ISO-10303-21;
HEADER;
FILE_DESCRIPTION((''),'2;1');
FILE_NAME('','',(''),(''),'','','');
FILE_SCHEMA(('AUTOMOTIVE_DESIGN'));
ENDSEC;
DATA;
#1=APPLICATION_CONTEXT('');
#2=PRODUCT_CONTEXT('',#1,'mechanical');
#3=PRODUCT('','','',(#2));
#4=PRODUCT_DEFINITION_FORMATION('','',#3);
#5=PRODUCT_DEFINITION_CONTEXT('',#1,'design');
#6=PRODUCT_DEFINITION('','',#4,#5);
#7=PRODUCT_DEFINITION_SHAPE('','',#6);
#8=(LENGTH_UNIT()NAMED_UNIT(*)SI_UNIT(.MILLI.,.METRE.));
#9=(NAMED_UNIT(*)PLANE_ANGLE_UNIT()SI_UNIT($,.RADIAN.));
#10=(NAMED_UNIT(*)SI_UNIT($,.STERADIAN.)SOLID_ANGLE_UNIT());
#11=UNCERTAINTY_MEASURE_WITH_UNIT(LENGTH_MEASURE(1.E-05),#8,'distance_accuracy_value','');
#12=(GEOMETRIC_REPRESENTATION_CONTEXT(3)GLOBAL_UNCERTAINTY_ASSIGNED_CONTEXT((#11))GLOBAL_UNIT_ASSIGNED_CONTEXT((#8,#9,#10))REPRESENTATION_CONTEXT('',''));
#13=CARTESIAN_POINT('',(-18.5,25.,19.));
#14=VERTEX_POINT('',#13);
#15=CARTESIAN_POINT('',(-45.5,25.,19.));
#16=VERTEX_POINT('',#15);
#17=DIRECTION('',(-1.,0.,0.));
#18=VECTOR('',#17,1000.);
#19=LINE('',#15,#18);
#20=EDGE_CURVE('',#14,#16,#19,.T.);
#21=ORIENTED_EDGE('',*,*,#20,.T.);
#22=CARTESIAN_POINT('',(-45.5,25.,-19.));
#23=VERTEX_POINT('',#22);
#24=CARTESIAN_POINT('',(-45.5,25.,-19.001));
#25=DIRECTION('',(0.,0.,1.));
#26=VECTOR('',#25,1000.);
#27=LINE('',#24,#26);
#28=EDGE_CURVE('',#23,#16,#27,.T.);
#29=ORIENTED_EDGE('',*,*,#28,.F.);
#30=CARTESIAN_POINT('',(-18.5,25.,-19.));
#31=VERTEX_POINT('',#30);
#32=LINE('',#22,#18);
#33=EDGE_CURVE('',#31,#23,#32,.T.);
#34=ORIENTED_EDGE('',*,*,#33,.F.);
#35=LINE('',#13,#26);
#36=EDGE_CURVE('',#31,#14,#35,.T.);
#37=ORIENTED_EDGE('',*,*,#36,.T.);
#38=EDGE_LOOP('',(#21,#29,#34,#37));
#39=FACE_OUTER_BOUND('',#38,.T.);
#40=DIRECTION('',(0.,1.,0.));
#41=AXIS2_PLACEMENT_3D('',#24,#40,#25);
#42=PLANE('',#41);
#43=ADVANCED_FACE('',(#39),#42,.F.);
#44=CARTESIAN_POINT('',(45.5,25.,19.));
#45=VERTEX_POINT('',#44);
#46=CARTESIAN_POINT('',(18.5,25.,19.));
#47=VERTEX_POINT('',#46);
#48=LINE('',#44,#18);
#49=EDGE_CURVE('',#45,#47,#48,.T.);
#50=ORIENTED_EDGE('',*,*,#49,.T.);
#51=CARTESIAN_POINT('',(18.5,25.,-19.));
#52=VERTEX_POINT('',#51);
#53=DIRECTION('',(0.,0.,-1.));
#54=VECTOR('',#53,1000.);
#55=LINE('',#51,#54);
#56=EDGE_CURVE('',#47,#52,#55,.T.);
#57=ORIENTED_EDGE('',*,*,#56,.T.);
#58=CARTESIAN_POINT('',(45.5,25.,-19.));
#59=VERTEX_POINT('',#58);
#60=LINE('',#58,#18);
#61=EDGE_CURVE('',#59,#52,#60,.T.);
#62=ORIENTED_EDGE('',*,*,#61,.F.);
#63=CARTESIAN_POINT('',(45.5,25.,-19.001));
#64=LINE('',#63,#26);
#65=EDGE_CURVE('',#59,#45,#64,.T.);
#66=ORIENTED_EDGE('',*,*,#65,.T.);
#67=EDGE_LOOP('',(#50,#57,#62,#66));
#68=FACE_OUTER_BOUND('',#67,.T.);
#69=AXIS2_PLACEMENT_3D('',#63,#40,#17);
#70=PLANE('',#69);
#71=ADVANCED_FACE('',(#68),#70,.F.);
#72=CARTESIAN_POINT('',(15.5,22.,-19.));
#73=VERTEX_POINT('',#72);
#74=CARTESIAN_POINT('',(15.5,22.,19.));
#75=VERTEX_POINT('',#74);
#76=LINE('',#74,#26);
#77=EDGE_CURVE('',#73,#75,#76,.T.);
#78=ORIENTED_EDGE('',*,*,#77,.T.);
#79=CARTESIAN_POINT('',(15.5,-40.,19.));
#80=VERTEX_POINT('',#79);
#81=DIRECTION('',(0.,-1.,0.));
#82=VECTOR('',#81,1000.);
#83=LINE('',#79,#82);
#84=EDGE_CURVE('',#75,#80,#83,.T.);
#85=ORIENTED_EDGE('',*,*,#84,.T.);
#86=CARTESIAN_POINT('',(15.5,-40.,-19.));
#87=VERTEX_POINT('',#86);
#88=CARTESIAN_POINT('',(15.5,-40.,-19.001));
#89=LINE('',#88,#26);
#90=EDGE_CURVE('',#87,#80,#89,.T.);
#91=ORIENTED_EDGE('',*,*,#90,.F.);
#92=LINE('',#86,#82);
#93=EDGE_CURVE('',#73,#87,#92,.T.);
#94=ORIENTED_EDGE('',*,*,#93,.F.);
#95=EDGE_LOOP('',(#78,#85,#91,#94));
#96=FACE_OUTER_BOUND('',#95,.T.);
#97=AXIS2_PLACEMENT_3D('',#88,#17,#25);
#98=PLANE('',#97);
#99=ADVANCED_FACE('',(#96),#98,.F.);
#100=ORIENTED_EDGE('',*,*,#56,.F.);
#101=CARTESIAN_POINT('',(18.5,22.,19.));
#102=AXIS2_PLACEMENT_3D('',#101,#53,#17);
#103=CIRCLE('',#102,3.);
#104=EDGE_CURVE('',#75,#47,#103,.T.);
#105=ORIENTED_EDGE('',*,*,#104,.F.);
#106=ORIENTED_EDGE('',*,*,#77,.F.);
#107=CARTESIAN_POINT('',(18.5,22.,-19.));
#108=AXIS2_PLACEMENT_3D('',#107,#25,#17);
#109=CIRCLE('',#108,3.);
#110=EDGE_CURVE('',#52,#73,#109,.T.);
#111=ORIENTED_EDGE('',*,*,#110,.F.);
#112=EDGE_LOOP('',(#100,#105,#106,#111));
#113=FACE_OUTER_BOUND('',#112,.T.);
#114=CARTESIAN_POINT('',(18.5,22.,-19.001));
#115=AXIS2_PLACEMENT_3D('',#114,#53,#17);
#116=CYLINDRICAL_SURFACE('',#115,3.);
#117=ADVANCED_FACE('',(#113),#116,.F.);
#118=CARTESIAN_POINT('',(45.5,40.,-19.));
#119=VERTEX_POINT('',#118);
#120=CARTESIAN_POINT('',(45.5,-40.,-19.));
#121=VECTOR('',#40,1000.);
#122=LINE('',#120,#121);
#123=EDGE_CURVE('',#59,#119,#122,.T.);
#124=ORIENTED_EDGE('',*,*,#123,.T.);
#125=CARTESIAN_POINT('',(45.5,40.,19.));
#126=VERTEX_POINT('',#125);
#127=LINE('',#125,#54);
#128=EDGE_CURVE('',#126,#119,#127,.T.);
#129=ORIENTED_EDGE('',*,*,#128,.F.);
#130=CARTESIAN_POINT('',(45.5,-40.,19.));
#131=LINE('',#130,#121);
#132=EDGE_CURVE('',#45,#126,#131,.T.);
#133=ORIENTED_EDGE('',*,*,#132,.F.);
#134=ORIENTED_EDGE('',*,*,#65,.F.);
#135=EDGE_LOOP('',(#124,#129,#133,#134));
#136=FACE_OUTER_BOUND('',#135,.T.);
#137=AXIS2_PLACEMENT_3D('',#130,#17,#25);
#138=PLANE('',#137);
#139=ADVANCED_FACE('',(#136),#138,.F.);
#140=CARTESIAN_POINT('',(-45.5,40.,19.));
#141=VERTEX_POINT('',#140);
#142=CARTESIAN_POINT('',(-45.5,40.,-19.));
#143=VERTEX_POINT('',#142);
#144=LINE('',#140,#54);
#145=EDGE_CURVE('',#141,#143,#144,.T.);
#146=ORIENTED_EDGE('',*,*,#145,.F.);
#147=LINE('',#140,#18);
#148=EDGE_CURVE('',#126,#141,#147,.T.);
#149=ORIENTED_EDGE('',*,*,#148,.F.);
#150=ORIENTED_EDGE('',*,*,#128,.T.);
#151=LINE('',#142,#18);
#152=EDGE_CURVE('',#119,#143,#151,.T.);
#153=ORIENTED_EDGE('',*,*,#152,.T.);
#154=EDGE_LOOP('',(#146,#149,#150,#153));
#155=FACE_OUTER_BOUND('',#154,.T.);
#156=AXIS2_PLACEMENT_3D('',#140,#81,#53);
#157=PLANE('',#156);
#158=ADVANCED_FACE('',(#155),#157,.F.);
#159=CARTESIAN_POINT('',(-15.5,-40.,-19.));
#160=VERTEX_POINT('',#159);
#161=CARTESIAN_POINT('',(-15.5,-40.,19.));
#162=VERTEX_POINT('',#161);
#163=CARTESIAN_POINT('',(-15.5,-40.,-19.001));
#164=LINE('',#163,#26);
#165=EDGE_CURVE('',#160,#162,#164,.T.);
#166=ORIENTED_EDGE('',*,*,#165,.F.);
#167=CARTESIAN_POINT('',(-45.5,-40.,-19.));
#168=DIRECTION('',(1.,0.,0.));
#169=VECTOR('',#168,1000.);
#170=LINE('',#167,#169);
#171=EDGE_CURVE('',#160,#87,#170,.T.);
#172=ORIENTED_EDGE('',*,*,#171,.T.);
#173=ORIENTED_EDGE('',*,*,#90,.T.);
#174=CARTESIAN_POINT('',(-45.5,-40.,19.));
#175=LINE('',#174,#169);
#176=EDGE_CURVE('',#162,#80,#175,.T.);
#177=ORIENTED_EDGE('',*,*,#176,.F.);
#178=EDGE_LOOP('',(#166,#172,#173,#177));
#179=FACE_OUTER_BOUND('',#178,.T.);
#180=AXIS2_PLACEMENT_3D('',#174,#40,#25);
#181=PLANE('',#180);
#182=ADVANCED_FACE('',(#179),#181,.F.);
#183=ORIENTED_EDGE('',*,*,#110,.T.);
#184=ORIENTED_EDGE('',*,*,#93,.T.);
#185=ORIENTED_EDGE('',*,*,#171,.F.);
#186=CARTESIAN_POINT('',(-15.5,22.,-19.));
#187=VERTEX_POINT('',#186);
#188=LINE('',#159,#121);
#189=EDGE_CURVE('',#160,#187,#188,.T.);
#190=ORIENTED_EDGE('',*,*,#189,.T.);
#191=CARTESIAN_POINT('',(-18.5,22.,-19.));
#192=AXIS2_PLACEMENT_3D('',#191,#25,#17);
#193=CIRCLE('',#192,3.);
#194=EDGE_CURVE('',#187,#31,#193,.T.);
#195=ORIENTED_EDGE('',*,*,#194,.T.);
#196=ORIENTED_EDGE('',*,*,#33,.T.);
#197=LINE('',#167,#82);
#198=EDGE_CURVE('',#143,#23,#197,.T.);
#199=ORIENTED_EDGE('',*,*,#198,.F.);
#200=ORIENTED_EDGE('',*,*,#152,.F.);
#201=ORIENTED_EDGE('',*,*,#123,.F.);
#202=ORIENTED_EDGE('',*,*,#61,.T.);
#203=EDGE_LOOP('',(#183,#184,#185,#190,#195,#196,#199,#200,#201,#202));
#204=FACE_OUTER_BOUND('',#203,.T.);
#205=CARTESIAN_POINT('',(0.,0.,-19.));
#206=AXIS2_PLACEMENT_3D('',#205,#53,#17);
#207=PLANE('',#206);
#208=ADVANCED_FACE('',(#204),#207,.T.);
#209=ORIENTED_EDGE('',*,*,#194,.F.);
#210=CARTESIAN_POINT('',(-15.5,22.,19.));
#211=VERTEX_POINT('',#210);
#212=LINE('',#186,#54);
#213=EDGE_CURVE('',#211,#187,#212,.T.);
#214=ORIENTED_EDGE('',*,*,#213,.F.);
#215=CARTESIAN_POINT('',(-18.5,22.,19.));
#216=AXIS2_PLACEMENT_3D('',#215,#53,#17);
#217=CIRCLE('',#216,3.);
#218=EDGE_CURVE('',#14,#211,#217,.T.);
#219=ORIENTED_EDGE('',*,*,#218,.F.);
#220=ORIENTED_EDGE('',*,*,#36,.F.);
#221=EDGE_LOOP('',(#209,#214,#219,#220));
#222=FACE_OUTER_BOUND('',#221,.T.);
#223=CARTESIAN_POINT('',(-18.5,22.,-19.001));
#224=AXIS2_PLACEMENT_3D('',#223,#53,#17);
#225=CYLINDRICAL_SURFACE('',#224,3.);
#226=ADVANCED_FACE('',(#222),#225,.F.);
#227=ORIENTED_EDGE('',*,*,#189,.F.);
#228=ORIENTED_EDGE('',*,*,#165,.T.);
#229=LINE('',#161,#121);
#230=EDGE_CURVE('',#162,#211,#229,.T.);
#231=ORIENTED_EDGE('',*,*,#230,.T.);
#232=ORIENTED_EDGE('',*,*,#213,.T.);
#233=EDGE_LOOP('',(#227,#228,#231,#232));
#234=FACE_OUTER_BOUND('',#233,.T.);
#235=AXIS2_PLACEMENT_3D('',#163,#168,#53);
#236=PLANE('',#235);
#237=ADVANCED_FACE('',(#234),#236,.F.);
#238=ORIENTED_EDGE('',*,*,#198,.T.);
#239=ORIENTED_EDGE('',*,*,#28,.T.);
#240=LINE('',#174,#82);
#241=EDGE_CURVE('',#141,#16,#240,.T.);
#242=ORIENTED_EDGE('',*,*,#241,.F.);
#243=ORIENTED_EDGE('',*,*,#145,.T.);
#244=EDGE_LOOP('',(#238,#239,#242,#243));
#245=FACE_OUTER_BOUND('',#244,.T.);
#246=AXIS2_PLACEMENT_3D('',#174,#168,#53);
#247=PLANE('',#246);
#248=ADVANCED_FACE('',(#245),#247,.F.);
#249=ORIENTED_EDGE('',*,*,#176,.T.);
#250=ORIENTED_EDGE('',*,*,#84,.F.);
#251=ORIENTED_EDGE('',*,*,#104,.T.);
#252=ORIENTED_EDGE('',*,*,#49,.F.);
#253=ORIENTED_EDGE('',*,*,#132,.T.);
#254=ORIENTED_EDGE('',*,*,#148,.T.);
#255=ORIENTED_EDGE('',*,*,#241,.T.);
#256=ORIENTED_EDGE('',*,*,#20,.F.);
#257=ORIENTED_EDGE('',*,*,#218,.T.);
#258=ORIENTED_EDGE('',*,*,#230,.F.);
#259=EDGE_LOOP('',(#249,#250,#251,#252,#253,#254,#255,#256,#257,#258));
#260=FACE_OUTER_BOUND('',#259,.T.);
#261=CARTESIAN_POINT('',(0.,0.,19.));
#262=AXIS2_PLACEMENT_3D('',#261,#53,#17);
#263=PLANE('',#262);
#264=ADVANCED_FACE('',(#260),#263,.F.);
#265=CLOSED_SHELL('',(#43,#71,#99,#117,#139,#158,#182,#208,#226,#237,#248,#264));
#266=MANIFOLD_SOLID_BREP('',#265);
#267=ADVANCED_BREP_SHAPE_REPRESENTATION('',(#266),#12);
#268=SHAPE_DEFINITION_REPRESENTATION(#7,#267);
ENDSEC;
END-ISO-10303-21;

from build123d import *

# Parameters (mm, degrees)
SKETCH_1_W          = 91
SKETCH_1_H          = 80
EXTRUDE_1_DEPTH     = 19
CUT_EXTRUDE_1_REACH = 73.514
SKETCH_2_W          = 30
SKETCH_2_H          = 65
FILLET_1_R          = 3


with BuildPart() as part:
    # 草图1 → 凸台-拉伸1 (new, symmetric)
    with BuildSketch(Plane.XY):
        Rectangle(SKETCH_1_W, SKETCH_1_H)
    extrude(amount=EXTRUDE_1_DEPTH, both=True)

    # 草图2 → 切除-拉伸1 (cut, up to next)
    with BuildSketch(Plane.XY.offset(19), mode=Mode.PRIVATE) as cut_extrude_1_sk1:
        with Locations((-30.5, -7.5)):
            Rectangle(SKETCH_2_W, SKETCH_2_H)
    cut_extrude_1_tool1 = extrude(cut_extrude_1_sk1.sketch, amount=-CUT_EXTRUDE_1_REACH, mode=Mode.PRIVATE) & part.part
    # 草图2 → 切除-拉伸1 (cut, up to next)
    with BuildSketch(Plane.XY.offset(19), mode=Mode.PRIVATE) as cut_extrude_1_sk2:
        with Locations((30.5, -7.5)):
            Rectangle(SKETCH_2_W, SKETCH_2_H)
    cut_extrude_1_tool2 = extrude(cut_extrude_1_sk2.sketch, amount=-CUT_EXTRUDE_1_REACH, mode=Mode.PRIVATE) & part.part
    add(cut_extrude_1_tool1.solids().sort_by_distance((-30.5, -7.5, 19))[0], mode=Mode.SUBTRACT)
    add(cut_extrude_1_tool2.solids().sort_by_distance((30.5, -7.5, 19))[0], mode=Mode.SUBTRACT)

    # 圆角1
    fillet_1_edges = [part.edges().sort_by_distance(p)[0] for p in [
        (-15.5, 25, 0),
        (15.5, 25, 0),
    ]]
    fillet(fillet_1_edges, radius=FILLET_1_R)


solid = part.part
